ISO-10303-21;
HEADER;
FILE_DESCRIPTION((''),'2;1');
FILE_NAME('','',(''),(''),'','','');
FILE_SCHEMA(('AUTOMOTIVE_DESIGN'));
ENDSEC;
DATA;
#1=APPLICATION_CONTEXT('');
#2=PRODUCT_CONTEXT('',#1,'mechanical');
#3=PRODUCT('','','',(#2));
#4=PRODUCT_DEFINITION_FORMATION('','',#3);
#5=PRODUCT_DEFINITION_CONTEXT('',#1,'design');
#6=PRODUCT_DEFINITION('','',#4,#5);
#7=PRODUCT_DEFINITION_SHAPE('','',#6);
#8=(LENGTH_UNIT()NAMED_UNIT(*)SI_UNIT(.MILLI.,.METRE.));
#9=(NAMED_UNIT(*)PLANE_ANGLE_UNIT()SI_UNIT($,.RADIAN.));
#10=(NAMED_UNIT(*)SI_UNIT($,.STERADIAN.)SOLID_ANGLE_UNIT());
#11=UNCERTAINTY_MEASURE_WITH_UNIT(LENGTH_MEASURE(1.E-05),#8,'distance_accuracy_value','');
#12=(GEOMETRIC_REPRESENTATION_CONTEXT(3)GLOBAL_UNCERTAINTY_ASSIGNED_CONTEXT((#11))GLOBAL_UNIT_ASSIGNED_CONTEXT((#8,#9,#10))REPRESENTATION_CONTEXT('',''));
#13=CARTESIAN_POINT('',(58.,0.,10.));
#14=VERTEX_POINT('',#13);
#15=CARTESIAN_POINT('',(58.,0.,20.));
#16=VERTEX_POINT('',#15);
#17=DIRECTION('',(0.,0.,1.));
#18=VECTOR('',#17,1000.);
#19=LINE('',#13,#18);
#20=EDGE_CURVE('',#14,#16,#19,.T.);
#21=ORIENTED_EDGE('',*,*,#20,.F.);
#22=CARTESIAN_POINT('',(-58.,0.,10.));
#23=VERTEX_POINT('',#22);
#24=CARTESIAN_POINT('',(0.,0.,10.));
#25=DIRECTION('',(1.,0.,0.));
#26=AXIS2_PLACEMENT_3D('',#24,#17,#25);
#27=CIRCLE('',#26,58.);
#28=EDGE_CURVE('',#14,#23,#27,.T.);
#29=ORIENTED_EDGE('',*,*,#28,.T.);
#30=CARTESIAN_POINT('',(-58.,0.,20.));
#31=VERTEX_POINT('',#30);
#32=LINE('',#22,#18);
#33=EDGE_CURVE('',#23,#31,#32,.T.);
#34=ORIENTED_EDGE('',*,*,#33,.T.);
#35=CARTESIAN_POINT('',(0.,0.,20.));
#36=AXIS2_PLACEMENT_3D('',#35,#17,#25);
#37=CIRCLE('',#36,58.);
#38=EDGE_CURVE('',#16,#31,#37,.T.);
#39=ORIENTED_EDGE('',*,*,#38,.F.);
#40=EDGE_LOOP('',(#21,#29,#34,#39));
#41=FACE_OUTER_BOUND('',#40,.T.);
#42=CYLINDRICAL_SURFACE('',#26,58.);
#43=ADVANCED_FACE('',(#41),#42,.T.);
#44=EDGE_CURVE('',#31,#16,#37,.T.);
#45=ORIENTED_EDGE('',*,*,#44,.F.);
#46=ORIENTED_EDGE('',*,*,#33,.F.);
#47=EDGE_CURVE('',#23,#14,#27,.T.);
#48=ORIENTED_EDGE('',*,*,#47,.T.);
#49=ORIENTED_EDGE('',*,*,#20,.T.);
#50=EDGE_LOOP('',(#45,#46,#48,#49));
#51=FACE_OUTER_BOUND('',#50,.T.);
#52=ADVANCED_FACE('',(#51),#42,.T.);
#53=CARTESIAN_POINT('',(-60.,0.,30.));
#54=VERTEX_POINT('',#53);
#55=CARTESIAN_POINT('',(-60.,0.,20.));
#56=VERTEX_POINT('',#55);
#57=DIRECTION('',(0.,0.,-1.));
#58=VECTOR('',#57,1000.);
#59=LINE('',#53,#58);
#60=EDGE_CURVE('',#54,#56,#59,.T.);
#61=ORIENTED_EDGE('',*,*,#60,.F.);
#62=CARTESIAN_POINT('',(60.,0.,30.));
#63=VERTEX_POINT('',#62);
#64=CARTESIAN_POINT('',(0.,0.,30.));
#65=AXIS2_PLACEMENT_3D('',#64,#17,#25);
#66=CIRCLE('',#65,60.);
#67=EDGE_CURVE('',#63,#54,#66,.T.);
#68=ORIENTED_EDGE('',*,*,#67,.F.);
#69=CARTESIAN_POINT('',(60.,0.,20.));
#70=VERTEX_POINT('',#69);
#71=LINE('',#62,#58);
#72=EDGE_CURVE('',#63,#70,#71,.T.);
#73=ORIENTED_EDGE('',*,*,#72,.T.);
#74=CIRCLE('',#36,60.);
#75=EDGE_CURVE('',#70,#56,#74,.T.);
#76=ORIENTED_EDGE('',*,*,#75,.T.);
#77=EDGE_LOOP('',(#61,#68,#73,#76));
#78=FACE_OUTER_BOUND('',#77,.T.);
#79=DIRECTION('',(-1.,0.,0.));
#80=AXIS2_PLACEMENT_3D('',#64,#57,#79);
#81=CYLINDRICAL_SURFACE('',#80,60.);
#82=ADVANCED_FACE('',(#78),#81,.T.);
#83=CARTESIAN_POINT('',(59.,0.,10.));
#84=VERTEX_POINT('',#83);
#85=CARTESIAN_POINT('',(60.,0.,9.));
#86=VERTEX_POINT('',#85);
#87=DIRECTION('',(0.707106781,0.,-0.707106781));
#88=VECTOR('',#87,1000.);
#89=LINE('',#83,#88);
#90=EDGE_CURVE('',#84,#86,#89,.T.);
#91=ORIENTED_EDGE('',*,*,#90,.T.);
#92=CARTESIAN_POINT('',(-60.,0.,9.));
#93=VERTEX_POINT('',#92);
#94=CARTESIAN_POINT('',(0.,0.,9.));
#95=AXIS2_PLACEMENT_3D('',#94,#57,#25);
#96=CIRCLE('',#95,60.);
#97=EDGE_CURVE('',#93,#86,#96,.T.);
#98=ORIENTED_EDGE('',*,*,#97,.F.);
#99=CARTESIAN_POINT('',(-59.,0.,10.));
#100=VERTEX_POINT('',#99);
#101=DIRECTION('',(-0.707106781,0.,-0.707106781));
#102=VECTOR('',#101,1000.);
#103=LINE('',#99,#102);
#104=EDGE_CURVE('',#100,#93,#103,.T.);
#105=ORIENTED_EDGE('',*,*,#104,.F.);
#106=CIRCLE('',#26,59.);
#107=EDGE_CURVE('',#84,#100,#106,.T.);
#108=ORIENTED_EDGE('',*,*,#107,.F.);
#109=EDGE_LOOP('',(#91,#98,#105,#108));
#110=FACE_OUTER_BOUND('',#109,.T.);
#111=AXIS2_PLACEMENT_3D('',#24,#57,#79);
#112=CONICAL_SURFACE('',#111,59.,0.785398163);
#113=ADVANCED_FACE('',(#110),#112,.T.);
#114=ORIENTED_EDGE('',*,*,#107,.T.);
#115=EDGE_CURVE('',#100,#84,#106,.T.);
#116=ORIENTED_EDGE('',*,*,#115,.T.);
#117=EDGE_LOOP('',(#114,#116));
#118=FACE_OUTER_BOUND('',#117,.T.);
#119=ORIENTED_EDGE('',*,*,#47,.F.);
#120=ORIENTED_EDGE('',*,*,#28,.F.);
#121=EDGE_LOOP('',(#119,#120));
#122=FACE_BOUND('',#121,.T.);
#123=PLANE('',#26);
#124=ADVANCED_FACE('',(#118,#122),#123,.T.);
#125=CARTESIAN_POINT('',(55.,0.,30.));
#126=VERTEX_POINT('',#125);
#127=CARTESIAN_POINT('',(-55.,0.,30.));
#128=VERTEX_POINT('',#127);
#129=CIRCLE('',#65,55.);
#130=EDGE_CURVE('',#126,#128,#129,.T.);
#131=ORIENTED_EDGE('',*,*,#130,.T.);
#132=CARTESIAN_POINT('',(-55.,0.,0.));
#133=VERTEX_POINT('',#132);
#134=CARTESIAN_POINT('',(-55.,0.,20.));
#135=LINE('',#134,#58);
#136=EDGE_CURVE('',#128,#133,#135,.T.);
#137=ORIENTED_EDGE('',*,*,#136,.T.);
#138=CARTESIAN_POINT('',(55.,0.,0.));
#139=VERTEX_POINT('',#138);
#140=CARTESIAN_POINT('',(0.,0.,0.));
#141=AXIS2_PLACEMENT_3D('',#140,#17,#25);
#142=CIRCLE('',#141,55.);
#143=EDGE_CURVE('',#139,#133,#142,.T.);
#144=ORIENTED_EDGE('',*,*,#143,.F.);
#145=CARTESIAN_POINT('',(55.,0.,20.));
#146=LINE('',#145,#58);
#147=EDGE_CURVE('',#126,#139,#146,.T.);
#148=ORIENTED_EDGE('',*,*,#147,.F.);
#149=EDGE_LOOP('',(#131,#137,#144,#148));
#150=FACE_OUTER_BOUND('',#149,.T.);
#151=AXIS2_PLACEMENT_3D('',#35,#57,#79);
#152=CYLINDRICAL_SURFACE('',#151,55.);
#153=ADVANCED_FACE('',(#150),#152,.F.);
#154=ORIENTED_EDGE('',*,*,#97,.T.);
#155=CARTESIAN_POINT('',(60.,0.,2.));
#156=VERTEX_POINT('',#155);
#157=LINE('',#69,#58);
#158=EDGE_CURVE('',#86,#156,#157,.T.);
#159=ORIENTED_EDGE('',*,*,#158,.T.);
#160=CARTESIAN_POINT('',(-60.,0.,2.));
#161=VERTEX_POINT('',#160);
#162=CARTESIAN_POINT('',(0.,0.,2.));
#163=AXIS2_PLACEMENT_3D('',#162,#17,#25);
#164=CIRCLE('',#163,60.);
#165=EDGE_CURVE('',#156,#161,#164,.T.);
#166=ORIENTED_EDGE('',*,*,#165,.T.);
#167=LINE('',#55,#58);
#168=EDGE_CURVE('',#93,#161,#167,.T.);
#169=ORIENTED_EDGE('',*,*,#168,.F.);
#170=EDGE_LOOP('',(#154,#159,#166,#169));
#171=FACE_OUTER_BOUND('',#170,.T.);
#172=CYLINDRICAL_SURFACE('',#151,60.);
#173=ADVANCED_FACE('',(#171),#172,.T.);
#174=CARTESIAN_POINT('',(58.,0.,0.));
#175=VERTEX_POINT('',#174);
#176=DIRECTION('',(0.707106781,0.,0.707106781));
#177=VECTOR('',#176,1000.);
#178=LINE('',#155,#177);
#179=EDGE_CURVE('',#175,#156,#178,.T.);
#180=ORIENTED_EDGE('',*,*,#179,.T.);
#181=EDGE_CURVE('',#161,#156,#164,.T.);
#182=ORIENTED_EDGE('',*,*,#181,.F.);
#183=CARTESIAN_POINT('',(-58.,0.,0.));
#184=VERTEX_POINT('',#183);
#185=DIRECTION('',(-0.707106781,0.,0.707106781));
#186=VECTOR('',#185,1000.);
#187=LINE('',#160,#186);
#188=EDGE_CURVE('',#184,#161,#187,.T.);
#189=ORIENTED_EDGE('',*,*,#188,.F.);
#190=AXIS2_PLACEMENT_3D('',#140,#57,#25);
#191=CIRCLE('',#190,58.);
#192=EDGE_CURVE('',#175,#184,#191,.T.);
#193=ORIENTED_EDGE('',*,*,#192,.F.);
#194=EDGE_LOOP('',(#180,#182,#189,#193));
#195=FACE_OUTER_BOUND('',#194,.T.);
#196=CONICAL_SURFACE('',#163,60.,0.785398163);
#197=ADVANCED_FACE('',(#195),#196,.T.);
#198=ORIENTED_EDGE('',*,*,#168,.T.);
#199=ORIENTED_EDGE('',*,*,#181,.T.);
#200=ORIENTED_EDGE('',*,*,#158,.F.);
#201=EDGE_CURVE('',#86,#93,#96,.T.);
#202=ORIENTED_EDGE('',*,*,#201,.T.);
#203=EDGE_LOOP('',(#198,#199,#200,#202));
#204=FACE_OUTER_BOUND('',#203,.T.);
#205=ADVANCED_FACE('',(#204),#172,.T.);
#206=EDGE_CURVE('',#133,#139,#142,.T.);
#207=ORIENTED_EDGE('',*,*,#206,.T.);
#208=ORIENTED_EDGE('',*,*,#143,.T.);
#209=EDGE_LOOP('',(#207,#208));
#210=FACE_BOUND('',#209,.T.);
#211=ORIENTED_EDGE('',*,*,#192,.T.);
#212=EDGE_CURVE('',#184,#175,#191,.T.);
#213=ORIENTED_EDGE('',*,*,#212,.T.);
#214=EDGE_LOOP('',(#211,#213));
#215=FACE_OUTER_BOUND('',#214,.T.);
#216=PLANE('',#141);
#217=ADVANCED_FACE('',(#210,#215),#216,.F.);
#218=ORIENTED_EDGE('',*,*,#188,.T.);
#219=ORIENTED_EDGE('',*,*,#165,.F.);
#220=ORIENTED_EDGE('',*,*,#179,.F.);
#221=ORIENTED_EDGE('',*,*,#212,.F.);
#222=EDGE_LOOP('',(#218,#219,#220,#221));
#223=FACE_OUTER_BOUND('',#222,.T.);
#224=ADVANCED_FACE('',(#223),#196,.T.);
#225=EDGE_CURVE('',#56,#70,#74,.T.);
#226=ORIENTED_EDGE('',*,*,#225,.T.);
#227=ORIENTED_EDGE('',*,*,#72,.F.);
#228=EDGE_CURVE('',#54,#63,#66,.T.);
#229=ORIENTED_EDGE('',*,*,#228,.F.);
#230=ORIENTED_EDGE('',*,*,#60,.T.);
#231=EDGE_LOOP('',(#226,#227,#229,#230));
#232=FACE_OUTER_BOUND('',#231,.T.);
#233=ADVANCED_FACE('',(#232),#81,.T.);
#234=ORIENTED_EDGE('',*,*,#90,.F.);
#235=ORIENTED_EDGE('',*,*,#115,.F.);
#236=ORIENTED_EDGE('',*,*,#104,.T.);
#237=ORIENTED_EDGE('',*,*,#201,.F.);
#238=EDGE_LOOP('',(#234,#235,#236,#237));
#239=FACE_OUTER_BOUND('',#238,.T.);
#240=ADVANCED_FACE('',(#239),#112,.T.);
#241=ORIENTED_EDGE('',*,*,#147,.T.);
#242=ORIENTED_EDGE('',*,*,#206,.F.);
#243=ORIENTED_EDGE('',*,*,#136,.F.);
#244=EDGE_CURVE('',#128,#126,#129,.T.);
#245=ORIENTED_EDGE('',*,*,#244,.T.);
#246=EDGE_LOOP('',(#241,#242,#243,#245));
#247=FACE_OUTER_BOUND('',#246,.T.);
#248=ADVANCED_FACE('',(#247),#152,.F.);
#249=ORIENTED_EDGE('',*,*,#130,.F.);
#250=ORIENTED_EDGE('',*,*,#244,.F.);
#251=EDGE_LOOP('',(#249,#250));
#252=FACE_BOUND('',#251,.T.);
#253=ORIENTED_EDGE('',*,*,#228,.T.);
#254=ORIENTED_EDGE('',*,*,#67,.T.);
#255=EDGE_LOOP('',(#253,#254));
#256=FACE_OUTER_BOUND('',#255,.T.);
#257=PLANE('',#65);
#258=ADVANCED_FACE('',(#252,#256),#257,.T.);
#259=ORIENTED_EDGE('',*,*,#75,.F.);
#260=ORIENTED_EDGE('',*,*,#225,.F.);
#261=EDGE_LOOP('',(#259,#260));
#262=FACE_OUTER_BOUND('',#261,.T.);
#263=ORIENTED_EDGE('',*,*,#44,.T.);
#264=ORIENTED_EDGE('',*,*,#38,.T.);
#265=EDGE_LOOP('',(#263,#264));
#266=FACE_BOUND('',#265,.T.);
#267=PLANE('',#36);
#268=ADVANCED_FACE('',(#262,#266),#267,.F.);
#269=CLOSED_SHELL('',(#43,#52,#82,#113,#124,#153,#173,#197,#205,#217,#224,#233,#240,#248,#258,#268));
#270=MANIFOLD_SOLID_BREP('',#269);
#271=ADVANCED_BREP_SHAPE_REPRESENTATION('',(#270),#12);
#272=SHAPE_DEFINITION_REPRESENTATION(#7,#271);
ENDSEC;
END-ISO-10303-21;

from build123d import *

# Parameters (mm, degrees)
SKETCH1_R           = 60
SKETCH1_R_2         = 55
BOSS_EXTRUDE1_DEPTH = 20
CUT_EXTRUDE1_START  = -10
SKETCH2_R           = 60
SKETCH2_R_2         = 58
CUT_EXTRUDE1_DEPTH  = 10
SKETCH3_R           = 60
SKETCH3_R_2         = 55
BOSS_EXTRUDE2_DEPTH = 10
CHAMFER1_SIZE       = 2
CHAMFER2_SIZE       = 1


with BuildPart() as part:
    # Sketch1 → Boss-Extrude1 (new body)
    with BuildSketch(Plane.XY):
        Circle(SKETCH1_R)
        Circle(SKETCH1_R_2, mode=Mode.SUBTRACT)
    extrude(amount=BOSS_EXTRUDE1_DEPTH)

    # Sketch2 → Cut-Extrude1 (cut)
    with BuildSketch(Plane.XY.offset(20).offset(CUT_EXTRUDE1_START)):
        Circle(SKETCH2_R)
        Circle(SKETCH2_R_2, mode=Mode.SUBTRACT)
    extrude(amount=CUT_EXTRUDE1_DEPTH, mode=Mode.SUBTRACT)

    # Sketch3 → Boss-Extrude2 (add)
    with BuildSketch(Plane.XY.offset(20)):
        Circle(SKETCH3_R)
        Circle(SKETCH3_R_2, mode=Mode.SUBTRACT)
    extrude(amount=BOSS_EXTRUDE2_DEPTH)

    # Chamfer1
    chamfer1_edges = [part.edges().sort_by_distance(p)[0] for p in [
        (-60, 0, 0),
    ]]
    chamfer(chamfer1_edges, length=CHAMFER1_SIZE)

    # Chamfer2
    chamfer2_edges = [part.edges().sort_by_distance(p)[0] for p in [
        (-60, 0, 10),
    ]]
    chamfer(chamfer2_edges, length=CHAMFER2_SIZE)


solid = part.part
